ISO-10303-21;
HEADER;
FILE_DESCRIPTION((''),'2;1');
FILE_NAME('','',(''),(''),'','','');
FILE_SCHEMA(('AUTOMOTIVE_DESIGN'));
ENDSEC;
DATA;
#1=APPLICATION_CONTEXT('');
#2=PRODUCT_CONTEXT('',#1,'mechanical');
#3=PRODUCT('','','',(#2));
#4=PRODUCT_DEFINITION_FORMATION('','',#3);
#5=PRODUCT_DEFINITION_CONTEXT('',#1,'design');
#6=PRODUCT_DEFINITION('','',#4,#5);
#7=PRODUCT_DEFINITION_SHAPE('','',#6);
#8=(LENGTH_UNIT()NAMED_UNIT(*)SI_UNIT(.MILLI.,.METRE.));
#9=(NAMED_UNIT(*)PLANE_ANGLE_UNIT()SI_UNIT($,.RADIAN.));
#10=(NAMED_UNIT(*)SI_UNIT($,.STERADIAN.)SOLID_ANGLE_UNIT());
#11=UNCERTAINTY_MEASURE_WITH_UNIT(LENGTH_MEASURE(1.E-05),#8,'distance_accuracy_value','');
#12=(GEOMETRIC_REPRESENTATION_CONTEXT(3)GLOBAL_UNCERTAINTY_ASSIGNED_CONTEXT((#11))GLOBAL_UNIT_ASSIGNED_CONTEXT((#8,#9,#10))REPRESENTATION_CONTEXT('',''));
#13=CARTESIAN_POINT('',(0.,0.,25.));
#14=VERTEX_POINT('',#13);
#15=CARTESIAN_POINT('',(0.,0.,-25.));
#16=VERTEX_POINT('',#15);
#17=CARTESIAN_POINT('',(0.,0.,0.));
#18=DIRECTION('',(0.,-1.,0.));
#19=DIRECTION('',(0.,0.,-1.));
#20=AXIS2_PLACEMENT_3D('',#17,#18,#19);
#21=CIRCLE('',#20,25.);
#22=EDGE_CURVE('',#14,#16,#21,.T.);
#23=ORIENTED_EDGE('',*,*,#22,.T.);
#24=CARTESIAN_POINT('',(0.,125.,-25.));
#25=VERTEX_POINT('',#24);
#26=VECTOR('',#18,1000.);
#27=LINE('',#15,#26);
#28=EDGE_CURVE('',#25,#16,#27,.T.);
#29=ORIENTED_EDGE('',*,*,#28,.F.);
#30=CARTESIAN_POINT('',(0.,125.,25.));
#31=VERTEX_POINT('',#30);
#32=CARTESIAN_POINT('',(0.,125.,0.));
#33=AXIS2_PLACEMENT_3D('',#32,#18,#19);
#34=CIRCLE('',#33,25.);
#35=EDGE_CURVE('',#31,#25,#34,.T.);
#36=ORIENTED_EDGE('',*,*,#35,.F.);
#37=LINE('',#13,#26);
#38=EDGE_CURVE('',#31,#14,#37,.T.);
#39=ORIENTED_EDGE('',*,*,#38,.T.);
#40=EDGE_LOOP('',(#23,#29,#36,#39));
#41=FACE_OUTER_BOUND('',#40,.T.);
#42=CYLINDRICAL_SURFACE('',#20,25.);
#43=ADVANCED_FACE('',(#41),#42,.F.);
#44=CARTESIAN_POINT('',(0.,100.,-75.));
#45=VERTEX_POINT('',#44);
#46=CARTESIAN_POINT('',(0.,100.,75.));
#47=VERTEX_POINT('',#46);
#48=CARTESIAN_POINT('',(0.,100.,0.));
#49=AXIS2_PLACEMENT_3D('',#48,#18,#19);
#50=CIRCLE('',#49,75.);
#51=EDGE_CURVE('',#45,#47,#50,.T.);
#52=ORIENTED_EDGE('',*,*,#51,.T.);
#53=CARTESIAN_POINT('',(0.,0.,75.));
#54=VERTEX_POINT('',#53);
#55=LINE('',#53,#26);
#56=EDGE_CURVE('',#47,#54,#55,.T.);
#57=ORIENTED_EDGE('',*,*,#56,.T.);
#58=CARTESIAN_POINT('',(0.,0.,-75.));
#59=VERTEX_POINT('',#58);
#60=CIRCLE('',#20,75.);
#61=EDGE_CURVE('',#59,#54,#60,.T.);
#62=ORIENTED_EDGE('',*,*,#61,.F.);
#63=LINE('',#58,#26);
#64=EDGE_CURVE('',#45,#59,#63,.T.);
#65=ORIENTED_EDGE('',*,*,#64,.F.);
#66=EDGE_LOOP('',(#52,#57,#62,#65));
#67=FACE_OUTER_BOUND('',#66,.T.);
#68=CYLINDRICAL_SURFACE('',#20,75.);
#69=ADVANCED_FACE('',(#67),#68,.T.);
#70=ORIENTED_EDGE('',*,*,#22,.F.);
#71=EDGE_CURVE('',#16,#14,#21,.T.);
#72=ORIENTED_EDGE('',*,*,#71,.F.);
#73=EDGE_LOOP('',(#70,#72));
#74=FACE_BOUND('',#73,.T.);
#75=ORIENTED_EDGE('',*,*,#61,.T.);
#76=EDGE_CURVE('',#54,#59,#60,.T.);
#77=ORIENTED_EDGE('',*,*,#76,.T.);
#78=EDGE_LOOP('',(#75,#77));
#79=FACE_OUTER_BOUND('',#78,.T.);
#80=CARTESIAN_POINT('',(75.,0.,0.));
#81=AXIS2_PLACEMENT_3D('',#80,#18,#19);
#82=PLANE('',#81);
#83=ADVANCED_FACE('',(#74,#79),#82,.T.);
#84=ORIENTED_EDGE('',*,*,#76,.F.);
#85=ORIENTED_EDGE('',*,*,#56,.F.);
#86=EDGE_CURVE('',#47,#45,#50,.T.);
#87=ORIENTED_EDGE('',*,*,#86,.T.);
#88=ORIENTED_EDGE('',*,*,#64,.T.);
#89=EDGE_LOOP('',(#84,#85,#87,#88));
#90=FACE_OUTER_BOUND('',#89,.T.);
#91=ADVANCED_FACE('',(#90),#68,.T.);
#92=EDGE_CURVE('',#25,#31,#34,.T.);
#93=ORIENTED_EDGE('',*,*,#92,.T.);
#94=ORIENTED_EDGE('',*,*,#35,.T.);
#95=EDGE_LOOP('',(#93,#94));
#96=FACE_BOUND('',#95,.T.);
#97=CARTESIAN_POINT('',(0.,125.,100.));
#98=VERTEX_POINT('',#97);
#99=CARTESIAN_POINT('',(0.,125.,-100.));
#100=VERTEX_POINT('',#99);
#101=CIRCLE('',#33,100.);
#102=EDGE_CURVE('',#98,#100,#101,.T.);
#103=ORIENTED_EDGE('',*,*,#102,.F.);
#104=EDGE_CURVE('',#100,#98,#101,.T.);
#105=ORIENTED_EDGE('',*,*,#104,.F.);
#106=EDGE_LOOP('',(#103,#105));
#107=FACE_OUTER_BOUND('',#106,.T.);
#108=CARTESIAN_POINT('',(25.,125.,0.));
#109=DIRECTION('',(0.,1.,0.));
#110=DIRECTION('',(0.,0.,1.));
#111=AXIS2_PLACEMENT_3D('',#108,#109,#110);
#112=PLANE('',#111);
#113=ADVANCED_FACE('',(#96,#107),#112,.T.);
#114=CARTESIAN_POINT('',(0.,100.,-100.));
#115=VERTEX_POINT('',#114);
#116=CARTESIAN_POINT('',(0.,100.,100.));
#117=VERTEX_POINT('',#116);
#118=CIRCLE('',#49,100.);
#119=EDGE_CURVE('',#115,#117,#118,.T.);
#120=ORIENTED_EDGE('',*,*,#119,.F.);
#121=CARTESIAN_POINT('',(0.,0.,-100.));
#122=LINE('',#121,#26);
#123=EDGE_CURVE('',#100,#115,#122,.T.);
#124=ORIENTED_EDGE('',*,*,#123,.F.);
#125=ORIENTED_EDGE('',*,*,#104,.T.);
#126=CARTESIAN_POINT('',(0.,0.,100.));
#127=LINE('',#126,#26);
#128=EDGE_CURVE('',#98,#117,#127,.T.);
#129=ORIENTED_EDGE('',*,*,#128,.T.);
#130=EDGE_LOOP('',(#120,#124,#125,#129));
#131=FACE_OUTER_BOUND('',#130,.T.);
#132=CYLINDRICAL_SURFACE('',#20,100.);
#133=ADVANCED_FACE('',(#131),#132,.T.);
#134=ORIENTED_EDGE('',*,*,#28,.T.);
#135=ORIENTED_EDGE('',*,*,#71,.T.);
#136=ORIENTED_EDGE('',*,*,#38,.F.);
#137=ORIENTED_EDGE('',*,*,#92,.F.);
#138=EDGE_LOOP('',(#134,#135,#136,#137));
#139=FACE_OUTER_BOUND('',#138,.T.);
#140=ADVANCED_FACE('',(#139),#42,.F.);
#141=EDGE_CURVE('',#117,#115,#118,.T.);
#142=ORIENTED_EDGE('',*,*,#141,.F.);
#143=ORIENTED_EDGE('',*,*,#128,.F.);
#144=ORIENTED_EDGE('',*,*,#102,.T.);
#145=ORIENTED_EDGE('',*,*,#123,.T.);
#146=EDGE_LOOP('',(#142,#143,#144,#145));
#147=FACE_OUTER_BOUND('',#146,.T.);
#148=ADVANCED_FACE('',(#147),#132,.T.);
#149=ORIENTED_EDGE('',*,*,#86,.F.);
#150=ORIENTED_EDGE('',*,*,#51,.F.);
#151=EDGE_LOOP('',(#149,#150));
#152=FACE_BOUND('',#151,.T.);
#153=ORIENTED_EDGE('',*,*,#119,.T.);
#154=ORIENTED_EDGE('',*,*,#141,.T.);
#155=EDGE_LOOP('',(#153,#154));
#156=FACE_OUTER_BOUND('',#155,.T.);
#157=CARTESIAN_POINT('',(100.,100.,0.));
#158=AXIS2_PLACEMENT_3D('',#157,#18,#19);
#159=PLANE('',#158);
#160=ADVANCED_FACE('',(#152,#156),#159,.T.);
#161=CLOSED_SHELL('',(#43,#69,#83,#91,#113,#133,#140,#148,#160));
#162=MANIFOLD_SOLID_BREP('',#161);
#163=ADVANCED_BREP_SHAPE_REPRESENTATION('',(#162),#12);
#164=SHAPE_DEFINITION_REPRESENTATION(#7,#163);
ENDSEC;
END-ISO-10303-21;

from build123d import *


with BuildPart() as part:
    # Bushing Half Profile → Flanged Bushing Revolve (revolve)
    with BuildSketch(Plane.XY, mode=Mode.PRIVATE) as flanged_bushing_revolve_sk:
        Polygon((25, 0), (25, 125), (100, 125), (100, 100), (75, 100), (75, 0), align=None)
    revolve(flanged_bushing_revolve_sk.sketch.rotate(Axis((0, 0, 0), (0, 1, 0)), 90), axis=Axis((0, 0, 0), (0, 1, 0)))


solid = part.part
